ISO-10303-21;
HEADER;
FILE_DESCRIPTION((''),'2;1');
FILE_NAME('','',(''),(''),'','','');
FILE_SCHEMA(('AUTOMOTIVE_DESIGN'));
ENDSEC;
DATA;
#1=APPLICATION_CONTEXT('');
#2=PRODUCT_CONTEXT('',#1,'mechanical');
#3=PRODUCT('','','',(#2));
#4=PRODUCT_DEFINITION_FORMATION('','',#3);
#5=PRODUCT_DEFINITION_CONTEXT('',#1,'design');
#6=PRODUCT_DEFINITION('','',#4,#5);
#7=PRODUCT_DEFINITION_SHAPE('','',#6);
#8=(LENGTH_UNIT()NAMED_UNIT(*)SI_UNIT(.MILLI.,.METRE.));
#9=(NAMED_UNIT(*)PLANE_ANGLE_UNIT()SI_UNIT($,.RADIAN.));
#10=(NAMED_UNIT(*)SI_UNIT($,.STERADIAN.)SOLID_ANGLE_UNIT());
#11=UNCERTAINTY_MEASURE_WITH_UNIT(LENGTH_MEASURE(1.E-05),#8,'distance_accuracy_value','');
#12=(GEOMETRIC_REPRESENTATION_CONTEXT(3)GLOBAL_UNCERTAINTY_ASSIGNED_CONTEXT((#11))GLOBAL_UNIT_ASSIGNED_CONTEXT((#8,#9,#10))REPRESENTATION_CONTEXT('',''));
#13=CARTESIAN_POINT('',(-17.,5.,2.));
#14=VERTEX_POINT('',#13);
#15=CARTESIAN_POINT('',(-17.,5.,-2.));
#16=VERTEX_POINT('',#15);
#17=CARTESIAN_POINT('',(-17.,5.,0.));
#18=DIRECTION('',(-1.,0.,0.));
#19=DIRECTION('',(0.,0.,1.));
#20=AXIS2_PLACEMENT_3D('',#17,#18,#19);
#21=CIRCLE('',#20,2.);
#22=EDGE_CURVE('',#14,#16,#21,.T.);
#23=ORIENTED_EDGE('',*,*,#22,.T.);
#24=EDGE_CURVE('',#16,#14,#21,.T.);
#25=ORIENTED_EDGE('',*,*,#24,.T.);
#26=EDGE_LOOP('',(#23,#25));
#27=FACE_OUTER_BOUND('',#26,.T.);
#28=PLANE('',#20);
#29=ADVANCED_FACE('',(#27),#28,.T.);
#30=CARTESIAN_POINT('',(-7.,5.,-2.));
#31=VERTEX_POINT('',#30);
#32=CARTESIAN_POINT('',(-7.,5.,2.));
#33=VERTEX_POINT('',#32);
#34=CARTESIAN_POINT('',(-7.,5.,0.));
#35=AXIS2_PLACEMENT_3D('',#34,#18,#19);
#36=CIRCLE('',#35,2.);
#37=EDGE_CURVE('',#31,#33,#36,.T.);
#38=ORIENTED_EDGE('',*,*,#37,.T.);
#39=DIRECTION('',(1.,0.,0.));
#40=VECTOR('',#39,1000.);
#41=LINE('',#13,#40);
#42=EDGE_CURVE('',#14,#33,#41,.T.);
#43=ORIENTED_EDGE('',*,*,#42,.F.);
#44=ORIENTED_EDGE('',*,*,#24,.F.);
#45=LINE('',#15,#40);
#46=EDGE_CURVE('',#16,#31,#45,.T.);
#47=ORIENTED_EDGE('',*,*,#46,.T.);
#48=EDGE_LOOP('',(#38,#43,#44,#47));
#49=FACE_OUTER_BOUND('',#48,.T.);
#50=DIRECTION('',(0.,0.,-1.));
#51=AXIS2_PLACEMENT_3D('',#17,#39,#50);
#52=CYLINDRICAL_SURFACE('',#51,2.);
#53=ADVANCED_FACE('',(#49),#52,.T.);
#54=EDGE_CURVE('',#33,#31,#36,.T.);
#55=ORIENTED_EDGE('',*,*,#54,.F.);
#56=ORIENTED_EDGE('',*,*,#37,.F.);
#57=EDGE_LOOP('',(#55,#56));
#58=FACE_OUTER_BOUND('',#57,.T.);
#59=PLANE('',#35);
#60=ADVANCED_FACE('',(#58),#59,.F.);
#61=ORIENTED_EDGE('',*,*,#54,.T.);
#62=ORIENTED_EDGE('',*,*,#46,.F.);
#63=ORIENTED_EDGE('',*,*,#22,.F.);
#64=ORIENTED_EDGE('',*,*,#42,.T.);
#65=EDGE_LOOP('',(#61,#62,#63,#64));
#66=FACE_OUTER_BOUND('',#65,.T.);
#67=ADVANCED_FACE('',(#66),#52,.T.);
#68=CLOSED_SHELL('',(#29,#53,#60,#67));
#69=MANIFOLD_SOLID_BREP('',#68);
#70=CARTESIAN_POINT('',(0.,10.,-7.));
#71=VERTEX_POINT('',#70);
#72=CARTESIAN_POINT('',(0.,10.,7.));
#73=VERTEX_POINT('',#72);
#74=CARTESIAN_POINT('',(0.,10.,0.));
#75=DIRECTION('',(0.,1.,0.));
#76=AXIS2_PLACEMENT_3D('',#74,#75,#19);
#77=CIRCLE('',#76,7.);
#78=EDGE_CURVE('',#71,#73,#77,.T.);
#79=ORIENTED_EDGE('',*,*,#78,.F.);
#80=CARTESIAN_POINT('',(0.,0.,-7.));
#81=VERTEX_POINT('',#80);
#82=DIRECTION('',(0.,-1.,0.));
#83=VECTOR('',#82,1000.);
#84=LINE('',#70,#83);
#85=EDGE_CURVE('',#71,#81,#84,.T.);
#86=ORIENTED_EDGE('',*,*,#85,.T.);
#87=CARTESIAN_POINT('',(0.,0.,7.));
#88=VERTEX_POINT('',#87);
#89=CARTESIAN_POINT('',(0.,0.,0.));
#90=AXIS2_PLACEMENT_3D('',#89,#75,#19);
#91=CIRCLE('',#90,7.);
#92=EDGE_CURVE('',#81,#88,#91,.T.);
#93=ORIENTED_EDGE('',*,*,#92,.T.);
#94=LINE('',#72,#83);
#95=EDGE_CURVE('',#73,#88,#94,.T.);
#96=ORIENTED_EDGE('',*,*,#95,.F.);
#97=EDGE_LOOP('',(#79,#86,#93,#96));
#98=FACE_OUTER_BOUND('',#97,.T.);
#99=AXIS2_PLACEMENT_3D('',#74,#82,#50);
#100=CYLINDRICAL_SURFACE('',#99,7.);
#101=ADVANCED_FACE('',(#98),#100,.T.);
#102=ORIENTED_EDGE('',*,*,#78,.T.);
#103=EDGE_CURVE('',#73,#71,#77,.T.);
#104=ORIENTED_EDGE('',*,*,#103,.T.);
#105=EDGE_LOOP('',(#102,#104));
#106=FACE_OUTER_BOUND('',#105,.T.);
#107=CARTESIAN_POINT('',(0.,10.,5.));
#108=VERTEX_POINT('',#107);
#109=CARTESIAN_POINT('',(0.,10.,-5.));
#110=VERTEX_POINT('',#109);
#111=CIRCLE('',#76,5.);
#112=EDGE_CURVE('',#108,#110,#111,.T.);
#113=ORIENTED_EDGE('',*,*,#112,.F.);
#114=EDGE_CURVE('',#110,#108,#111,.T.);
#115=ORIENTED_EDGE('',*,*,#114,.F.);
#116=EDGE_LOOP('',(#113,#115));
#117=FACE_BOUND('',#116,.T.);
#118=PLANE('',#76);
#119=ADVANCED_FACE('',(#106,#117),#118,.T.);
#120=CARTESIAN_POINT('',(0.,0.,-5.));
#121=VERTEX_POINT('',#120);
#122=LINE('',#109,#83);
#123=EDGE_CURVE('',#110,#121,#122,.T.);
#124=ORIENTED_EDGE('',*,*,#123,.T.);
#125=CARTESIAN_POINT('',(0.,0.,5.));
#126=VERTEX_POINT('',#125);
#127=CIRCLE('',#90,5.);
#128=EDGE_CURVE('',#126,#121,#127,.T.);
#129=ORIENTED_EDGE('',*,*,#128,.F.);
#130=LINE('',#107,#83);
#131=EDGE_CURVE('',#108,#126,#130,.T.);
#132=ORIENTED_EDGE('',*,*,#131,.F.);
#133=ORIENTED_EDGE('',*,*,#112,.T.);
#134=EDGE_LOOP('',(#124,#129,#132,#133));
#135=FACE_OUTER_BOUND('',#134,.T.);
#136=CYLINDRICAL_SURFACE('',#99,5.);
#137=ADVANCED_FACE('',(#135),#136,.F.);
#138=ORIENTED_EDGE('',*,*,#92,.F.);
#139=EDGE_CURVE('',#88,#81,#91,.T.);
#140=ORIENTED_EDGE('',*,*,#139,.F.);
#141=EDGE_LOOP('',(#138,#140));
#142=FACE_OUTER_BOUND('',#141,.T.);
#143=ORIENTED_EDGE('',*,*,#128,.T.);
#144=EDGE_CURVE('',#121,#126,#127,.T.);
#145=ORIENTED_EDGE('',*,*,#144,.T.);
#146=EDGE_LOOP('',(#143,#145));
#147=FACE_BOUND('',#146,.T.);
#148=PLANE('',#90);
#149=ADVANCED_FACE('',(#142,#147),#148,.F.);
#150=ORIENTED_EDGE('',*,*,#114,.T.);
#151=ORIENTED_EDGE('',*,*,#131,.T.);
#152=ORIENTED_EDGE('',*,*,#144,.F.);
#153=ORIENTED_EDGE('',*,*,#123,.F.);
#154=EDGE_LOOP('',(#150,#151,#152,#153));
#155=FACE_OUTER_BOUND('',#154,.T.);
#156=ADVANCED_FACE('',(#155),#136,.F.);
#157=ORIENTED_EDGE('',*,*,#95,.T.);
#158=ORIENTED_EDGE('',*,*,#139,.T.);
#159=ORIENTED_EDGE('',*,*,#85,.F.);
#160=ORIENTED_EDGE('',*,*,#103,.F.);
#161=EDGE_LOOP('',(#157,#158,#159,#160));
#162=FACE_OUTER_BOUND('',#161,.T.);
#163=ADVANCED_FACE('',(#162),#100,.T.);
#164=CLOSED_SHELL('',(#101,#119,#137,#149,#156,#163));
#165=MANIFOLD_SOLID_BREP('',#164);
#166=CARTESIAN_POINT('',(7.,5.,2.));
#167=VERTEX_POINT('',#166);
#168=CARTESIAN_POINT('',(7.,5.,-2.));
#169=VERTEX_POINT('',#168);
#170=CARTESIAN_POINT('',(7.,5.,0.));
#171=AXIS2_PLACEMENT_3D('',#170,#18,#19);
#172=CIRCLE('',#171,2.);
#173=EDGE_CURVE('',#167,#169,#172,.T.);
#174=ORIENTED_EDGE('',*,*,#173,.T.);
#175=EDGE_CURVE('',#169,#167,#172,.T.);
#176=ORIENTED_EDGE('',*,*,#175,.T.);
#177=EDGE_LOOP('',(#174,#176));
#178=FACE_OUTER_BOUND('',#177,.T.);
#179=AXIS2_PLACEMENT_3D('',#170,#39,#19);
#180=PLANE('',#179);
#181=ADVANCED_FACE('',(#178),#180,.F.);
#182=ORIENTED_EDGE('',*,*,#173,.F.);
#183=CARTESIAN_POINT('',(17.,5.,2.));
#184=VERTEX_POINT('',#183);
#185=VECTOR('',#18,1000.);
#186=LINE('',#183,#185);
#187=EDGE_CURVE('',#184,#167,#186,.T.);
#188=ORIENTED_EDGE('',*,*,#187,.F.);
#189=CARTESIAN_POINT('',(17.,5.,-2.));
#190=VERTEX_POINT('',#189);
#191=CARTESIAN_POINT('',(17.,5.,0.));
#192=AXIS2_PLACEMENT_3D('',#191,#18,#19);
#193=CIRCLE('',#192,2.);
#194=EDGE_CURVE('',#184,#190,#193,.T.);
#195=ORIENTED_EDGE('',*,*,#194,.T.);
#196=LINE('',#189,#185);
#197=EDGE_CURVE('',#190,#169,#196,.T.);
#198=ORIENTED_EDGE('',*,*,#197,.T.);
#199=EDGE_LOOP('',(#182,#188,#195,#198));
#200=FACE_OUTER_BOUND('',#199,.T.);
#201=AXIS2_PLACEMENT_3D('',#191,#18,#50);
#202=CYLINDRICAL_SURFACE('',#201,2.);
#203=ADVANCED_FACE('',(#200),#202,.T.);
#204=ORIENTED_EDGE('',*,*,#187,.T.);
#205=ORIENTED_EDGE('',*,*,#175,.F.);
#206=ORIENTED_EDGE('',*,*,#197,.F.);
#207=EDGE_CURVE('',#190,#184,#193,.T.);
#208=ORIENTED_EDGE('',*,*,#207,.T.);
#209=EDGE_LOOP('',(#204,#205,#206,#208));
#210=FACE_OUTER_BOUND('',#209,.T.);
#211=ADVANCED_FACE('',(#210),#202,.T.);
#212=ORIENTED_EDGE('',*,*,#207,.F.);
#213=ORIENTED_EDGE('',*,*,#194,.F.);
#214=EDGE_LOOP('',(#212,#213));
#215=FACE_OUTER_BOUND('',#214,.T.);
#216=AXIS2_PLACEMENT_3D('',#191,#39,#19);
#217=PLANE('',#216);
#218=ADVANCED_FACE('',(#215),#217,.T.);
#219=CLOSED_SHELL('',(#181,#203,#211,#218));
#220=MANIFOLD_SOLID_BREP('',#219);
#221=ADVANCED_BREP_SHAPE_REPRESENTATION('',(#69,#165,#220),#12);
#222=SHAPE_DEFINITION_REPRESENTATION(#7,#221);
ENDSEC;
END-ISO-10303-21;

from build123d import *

# Parameters (mm, degrees)
SKETCH_2_R      = 7
SKETCH_2_R_2    = 5
EXTRUDE_1_DEPTH = 10
SKETCH_3_R      = 2
EXTRUDE_2_DEPTH = 10


with BuildPart() as part:
    # 草图2 → 凸台-拉伸1 (new body)
    with BuildSketch(Plane(origin=(0, 0, 0), x_dir=(1, 0, 0), z_dir=(0, 1, 0))):
        with Locations(Location((0, 0, 0), (0, 0, 270))):
            Circle(SKETCH_2_R)
        with Locations(Location((0, 0, 0), (0, 0, 270))):
            Circle(SKETCH_2_R_2, mode=Mode.SUBTRACT)
    extrude(amount=EXTRUDE_1_DEPTH)


with BuildPart() as body_2:
    # 草图3 → 凸台-拉伸2 (new body)
    with BuildSketch(Plane.ZY.offset(7)):
        with Locations((0, 5)):
            Circle(SKETCH_3_R)
    extrude(amount=EXTRUDE_2_DEPTH)


with BuildPart() as body_3:
    # 镜向3: mirrored copy
    add(body_2.part.mirror(Plane(origin=(0, 0, 0), x_dir=(0, 0, 1), z_dir=(1, 0, 0))))


solid = Compound([part.part, body_2.part, body_3.part])
